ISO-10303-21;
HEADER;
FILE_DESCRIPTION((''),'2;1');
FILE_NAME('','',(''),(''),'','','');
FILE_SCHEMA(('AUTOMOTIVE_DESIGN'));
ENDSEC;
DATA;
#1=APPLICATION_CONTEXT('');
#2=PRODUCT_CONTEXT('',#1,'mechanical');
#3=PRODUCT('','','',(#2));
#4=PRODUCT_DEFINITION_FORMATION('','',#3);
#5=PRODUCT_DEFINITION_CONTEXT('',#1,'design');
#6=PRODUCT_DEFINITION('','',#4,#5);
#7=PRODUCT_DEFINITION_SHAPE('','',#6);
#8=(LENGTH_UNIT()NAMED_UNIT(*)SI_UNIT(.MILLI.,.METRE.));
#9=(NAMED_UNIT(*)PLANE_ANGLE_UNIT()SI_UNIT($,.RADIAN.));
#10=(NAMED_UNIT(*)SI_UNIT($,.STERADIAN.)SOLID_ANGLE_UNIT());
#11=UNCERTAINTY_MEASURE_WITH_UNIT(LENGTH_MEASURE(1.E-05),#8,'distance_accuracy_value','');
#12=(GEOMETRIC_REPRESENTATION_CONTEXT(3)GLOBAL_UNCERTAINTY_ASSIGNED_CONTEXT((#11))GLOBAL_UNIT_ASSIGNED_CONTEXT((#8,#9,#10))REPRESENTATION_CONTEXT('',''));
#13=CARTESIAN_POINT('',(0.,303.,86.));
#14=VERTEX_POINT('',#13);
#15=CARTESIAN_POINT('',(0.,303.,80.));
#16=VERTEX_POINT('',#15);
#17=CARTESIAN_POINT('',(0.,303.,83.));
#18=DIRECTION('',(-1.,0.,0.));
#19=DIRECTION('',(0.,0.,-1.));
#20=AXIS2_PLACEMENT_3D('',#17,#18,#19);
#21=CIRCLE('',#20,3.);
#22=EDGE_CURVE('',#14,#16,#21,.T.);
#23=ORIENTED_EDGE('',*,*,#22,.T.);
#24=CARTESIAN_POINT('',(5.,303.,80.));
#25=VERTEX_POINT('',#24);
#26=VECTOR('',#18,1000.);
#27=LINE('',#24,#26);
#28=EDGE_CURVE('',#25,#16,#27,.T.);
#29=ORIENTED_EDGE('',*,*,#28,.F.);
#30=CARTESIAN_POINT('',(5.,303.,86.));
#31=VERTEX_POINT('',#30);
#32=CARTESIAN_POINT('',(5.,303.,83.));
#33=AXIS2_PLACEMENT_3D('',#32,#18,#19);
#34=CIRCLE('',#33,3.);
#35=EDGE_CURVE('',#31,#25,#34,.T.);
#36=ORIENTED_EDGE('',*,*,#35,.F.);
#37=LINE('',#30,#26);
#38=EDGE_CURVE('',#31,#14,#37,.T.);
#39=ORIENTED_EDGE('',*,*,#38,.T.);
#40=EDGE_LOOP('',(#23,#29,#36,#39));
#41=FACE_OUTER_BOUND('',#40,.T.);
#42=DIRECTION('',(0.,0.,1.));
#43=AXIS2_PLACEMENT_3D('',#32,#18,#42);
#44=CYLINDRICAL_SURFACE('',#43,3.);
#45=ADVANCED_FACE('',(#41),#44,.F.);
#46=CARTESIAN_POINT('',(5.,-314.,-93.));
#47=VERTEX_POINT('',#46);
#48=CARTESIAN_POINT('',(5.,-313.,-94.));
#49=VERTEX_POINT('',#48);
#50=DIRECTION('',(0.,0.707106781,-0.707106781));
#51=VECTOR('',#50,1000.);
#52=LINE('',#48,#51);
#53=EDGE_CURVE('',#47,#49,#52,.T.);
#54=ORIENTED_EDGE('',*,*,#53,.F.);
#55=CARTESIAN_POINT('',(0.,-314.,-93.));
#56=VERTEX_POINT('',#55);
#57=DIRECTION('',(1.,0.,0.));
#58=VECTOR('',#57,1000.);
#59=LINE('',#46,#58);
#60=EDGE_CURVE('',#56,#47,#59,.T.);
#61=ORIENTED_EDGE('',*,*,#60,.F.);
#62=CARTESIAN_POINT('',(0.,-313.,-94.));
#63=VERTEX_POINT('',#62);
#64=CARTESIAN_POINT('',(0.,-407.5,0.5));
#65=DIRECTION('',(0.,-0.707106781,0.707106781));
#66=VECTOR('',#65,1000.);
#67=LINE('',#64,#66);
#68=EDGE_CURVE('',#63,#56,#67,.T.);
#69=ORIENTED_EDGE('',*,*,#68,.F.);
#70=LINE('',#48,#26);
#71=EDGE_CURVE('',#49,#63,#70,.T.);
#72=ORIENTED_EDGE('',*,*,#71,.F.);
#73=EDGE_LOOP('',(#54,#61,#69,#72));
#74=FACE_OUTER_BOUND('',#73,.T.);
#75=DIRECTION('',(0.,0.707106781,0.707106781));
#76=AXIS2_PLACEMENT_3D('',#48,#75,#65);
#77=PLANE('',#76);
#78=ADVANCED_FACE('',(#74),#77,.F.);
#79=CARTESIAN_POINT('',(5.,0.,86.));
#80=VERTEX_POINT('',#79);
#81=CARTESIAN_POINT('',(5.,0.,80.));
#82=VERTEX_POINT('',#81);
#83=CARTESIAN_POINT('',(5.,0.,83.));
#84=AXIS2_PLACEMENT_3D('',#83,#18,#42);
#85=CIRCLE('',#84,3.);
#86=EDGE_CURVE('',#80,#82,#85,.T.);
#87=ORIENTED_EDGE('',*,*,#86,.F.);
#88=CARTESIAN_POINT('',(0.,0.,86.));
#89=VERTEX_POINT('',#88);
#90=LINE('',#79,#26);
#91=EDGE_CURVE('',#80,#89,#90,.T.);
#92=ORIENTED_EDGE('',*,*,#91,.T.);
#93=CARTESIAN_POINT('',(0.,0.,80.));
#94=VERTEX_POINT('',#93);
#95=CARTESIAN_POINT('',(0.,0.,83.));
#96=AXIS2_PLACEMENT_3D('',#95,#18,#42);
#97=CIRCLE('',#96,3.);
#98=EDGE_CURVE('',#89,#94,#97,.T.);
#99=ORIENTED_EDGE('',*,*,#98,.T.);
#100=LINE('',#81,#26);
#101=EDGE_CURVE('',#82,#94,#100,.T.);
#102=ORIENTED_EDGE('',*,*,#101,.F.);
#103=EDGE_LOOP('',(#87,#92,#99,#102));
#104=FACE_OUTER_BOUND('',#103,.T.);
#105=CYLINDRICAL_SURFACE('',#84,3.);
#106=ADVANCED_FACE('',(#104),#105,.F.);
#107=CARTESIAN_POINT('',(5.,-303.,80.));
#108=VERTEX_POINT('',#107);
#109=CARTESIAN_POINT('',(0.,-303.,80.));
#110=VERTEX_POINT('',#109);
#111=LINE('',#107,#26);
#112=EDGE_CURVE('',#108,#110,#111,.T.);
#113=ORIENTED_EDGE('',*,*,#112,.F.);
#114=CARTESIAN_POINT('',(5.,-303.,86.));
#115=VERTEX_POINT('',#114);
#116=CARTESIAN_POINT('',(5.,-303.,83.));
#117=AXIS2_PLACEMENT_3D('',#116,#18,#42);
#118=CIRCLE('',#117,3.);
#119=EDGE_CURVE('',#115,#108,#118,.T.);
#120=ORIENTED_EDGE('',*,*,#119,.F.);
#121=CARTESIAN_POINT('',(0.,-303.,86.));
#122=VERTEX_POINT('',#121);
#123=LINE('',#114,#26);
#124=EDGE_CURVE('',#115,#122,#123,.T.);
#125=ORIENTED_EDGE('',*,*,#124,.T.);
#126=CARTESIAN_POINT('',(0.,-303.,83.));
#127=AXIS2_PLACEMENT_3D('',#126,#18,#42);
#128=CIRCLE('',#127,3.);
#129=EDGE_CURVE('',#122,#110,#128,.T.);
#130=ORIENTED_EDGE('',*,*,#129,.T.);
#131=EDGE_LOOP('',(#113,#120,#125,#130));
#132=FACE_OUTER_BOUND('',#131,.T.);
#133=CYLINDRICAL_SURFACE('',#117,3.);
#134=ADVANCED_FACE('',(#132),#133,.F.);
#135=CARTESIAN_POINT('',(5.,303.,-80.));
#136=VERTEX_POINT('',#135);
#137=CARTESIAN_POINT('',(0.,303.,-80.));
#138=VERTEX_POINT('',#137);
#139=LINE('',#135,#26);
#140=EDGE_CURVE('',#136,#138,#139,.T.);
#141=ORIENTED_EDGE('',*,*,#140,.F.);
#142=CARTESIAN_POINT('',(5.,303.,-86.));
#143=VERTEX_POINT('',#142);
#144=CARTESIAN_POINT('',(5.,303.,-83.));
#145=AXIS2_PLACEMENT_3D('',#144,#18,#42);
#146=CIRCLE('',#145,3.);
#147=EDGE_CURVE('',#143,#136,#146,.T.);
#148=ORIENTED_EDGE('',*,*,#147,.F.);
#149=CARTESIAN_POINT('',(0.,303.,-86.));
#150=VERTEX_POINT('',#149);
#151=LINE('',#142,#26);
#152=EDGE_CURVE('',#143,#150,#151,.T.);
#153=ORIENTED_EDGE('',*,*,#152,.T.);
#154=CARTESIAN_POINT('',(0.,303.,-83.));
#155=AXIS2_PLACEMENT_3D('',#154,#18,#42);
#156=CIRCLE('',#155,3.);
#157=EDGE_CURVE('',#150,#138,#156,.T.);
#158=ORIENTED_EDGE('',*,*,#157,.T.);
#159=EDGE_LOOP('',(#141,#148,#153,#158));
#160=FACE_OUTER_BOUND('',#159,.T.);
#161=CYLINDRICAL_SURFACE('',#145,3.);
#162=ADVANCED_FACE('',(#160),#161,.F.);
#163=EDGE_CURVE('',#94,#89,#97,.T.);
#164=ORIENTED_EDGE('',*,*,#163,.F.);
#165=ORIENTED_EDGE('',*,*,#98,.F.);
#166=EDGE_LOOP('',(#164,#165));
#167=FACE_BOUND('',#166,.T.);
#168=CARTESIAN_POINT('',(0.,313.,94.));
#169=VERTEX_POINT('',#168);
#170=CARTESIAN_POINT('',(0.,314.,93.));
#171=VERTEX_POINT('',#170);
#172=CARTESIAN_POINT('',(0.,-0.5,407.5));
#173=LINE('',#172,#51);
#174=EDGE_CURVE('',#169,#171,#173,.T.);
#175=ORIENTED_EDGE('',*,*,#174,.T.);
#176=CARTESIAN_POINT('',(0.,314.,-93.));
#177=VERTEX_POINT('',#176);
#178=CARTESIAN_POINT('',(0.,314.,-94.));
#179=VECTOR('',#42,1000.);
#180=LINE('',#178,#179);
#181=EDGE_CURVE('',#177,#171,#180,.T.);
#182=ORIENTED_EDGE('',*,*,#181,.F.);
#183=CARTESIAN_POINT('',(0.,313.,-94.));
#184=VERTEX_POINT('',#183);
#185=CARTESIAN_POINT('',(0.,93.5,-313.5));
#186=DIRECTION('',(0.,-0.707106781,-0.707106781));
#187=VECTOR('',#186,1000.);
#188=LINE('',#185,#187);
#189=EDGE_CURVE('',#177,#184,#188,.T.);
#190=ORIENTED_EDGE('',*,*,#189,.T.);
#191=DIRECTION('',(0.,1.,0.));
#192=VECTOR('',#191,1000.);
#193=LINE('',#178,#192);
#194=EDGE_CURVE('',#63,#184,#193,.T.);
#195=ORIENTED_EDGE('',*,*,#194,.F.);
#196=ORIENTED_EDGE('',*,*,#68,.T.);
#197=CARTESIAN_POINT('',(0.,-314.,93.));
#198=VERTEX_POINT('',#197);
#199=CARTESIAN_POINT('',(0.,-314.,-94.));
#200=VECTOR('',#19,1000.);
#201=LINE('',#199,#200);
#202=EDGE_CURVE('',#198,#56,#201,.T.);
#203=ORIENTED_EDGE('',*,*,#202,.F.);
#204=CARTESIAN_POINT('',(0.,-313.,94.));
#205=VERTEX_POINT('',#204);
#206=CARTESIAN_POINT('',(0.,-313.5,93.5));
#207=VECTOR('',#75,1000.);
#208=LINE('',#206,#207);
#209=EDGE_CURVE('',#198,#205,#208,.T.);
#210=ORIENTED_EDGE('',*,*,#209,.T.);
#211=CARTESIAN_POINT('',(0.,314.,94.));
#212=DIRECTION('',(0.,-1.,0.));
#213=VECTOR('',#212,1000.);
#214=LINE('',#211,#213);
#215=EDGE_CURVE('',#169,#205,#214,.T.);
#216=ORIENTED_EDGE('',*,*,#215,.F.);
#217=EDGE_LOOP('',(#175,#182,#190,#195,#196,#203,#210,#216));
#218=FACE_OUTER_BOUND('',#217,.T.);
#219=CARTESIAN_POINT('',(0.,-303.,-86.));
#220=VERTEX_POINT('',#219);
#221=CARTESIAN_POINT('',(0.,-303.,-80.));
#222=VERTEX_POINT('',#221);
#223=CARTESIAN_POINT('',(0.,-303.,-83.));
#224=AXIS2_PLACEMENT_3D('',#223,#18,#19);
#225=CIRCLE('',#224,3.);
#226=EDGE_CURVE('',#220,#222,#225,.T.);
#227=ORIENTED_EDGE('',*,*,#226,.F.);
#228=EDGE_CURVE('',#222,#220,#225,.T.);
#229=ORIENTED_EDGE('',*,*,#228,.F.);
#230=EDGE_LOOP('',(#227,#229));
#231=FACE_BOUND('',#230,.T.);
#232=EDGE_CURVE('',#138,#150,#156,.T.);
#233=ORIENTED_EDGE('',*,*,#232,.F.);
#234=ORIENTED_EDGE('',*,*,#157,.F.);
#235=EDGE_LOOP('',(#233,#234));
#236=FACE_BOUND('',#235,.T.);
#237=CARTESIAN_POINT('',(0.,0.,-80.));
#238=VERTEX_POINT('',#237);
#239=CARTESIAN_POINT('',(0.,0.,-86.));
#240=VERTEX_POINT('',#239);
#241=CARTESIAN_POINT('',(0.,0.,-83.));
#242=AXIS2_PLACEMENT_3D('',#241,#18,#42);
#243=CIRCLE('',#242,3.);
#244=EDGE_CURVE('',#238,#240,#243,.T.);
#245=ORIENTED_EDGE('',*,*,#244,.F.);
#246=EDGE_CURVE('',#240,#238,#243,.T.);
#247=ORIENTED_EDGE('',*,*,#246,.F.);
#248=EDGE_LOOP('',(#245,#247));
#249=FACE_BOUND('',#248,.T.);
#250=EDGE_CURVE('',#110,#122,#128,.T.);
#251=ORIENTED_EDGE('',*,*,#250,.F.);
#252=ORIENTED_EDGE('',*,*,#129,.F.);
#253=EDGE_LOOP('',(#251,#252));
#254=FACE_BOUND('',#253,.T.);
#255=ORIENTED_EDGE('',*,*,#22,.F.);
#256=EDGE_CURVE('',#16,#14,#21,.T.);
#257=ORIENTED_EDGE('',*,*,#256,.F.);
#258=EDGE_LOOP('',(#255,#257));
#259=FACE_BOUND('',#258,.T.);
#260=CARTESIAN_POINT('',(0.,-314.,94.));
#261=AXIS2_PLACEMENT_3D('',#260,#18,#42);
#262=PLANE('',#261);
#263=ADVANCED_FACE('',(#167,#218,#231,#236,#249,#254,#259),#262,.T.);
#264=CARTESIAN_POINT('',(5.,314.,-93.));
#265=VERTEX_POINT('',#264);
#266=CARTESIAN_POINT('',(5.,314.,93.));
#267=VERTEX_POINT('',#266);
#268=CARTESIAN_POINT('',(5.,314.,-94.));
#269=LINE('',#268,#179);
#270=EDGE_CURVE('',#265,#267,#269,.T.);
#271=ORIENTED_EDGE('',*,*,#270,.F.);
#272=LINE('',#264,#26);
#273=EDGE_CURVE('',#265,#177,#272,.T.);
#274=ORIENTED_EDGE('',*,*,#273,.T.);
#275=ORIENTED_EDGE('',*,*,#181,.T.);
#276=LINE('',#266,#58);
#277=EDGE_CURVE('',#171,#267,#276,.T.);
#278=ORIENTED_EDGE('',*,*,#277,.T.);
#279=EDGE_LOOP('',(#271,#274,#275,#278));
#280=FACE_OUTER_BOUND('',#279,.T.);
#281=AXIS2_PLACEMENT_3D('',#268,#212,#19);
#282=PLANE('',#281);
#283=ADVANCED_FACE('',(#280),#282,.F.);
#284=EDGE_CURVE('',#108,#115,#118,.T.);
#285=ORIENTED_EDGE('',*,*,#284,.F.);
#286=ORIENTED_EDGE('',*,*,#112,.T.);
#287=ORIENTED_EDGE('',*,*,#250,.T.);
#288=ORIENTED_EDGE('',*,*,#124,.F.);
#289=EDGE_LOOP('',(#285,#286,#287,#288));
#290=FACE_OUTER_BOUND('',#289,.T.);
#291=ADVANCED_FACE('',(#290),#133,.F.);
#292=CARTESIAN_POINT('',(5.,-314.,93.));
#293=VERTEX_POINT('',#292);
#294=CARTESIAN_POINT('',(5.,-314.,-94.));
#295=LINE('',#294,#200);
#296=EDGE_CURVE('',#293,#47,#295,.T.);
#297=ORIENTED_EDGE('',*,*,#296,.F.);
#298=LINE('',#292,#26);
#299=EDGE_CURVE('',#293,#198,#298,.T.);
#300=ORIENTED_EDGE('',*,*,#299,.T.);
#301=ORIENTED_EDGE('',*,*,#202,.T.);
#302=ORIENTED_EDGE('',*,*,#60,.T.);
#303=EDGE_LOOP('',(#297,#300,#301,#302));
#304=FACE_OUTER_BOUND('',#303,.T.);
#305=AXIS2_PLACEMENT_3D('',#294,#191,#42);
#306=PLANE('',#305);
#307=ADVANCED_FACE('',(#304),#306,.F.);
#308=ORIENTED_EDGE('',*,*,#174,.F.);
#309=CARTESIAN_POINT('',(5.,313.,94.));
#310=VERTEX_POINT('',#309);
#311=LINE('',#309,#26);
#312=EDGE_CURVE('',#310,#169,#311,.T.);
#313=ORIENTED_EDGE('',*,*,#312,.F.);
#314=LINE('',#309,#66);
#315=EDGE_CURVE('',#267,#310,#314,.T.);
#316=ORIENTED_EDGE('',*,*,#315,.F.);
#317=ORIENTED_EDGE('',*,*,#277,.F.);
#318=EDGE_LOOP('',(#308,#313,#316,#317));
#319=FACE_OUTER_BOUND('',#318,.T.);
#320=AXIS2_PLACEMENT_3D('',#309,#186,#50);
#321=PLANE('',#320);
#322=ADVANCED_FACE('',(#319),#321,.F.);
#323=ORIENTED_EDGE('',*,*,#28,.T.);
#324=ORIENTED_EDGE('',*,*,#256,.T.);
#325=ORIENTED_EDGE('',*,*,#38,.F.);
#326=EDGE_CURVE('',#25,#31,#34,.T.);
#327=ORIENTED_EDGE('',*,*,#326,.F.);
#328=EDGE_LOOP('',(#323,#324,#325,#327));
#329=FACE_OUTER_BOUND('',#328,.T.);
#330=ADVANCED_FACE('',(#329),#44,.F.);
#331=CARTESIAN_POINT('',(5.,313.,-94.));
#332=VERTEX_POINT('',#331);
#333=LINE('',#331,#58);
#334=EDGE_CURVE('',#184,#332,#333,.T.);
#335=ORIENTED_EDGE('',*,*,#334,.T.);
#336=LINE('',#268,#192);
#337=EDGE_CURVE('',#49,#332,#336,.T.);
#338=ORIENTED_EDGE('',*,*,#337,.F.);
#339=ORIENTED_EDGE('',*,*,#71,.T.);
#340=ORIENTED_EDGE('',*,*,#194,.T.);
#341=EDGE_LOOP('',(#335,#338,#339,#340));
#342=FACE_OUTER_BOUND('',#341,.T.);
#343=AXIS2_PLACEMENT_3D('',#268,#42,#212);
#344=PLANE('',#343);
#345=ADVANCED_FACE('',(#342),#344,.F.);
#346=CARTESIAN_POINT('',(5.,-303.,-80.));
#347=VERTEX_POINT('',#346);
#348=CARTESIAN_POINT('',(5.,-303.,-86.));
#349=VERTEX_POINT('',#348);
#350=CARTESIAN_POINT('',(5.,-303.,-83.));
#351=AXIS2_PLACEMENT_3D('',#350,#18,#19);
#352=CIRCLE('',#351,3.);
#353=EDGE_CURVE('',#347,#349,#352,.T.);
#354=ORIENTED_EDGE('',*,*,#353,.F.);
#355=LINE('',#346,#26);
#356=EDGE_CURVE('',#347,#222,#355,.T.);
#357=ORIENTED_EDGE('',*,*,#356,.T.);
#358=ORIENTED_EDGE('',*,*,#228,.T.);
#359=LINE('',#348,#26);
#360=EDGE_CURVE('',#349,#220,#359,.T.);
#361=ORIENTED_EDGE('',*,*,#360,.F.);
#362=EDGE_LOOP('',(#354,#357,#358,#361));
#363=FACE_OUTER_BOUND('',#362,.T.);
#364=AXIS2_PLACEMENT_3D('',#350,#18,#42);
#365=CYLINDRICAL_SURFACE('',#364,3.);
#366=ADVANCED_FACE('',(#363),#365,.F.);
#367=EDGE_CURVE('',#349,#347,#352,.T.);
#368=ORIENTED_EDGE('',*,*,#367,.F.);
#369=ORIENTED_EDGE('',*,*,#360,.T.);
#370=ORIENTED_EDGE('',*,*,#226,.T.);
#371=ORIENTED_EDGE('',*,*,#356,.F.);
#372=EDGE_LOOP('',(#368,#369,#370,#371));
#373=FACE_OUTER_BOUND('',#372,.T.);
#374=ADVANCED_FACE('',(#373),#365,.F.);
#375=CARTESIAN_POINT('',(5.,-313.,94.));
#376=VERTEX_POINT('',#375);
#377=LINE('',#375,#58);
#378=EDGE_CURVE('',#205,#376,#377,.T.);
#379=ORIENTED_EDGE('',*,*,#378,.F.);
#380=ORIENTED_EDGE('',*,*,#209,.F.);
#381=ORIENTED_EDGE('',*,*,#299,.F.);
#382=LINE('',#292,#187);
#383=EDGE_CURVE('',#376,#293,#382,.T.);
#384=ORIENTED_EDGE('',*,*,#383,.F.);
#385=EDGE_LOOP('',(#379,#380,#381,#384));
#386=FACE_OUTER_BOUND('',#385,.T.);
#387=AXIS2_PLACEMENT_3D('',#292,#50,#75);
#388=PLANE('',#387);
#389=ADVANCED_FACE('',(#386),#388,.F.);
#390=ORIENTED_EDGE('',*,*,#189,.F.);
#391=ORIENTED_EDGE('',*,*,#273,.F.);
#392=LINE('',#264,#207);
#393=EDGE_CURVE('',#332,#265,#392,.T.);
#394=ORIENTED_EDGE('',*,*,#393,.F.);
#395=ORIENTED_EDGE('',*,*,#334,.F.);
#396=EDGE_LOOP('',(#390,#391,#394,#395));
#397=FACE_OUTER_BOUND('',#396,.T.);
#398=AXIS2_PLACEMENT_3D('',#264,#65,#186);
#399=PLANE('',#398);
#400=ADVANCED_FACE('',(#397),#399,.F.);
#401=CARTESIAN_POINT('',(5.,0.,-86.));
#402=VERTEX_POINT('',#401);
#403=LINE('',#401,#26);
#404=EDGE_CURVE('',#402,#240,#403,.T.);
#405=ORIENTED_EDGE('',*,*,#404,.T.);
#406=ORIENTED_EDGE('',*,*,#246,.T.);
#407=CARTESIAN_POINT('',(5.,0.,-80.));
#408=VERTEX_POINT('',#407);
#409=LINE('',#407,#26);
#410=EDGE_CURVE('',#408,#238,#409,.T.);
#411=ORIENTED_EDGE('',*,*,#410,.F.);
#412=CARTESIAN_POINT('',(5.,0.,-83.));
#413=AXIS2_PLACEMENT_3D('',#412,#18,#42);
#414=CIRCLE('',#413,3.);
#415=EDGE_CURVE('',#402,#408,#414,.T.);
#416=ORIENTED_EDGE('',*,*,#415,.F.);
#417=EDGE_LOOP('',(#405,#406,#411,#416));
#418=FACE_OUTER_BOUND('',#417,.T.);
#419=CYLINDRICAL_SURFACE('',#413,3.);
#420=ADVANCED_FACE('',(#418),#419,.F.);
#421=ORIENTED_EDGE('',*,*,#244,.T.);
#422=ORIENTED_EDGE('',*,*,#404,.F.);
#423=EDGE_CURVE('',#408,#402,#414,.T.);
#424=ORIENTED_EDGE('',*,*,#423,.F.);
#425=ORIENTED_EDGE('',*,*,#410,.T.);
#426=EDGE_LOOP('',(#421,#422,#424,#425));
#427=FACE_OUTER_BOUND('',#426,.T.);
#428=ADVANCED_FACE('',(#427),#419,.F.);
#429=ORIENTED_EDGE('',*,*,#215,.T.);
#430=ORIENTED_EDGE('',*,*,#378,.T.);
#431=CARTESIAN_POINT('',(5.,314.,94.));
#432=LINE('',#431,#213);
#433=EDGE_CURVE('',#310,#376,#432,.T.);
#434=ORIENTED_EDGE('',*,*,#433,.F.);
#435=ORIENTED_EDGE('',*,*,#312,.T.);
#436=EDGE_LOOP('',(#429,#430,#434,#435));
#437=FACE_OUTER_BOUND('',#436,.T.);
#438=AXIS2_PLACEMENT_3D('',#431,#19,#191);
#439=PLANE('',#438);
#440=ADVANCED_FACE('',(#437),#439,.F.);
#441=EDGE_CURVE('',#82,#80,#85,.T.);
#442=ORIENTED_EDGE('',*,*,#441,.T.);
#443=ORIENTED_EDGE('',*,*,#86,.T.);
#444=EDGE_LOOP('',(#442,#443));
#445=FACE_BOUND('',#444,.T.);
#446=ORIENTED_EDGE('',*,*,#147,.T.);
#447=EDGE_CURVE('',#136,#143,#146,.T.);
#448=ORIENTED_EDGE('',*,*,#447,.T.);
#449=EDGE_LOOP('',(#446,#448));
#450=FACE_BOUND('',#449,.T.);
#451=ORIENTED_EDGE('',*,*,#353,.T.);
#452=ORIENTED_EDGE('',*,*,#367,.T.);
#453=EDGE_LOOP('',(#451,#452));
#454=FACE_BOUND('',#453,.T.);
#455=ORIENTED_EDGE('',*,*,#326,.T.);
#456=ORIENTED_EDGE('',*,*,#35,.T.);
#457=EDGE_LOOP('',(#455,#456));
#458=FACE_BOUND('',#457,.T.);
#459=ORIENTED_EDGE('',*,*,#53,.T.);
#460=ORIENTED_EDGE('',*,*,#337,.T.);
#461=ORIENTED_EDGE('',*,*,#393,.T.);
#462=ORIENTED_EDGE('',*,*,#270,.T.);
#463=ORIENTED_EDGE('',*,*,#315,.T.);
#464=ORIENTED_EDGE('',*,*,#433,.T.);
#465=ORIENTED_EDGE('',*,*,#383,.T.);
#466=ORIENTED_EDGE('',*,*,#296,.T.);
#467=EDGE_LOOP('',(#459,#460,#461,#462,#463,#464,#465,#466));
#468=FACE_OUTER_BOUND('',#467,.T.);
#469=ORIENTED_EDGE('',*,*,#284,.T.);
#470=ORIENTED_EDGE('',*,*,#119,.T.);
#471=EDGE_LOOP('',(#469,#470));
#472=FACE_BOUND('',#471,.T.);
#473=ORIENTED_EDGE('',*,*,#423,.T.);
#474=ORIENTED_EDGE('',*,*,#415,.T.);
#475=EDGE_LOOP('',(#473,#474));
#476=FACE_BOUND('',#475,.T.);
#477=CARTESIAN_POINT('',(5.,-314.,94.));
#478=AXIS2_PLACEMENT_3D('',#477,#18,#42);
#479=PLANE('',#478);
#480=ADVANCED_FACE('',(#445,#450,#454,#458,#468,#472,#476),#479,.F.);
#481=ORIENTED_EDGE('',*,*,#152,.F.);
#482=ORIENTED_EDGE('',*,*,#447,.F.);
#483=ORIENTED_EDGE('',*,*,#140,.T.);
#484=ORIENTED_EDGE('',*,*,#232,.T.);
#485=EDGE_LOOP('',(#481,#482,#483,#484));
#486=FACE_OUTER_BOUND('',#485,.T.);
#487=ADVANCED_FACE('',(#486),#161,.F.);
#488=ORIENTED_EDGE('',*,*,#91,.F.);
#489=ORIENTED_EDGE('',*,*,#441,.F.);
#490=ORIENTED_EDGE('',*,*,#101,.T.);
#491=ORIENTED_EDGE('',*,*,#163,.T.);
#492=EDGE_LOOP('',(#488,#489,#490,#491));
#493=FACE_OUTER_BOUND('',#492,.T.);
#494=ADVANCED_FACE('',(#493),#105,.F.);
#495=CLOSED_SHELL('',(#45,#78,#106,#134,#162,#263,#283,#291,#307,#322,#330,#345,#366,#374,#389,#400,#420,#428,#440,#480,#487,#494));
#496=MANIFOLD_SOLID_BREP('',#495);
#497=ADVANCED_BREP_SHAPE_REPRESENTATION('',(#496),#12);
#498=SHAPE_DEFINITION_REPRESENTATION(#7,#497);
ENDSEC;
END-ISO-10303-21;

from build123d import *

# Parameters (mm, degrees)
SKETCH_1_W          = 188
SKETCH_1_H          = 628
EXTRUDE_1_DEPTH     = 5
CHAMFER_1_SIZE      = 1
SKETCH_2_R          = 3
CUT_EXTRUDE_1_DEPTH = 328.806345271


with BuildPart() as part:
    # 草图1 → 凸台-拉伸1 (new body)
    with BuildSketch(Plane(origin=(0, 0, 0), x_dir=(0, 0, -1), z_dir=(1, 0, 0))):
        Rectangle(SKETCH_1_W, SKETCH_1_H)
    extrude(amount=EXTRUDE_1_DEPTH)

    # 倒角1
    chamfer_1_edges = [part.edges().sort_by_distance(p)[0] for p in [
        (2.5, 314, 94),
        (2.5, 314, -94),
        (2.5, -314, -94),
        (2.5, -314, 94),
    ]]
    chamfer(chamfer_1_edges, length=CHAMFER_1_SIZE)

    # 草图2 → 切除-拉伸1 (cut, through all)
    with BuildSketch(Plane.ZY):
        with Locations((-83, 303)):
            Circle(SKETCH_2_R)
        with Locations(Location((-83, -303, 0), (0, 0, 180))):
            Circle(SKETCH_2_R)
        with Locations((83, -303)):
            Circle(SKETCH_2_R)
        with Locations(Location((83, 303, 0), (0, 0, 180))):
            Circle(SKETCH_2_R)
        with Locations((83, 0)):
            Circle(SKETCH_2_R)
        with Locations((-83, 0)):
            Circle(SKETCH_2_R)
    extrude(amount=-CUT_EXTRUDE_1_DEPTH, mode=Mode.SUBTRACT)


solid = part.part
